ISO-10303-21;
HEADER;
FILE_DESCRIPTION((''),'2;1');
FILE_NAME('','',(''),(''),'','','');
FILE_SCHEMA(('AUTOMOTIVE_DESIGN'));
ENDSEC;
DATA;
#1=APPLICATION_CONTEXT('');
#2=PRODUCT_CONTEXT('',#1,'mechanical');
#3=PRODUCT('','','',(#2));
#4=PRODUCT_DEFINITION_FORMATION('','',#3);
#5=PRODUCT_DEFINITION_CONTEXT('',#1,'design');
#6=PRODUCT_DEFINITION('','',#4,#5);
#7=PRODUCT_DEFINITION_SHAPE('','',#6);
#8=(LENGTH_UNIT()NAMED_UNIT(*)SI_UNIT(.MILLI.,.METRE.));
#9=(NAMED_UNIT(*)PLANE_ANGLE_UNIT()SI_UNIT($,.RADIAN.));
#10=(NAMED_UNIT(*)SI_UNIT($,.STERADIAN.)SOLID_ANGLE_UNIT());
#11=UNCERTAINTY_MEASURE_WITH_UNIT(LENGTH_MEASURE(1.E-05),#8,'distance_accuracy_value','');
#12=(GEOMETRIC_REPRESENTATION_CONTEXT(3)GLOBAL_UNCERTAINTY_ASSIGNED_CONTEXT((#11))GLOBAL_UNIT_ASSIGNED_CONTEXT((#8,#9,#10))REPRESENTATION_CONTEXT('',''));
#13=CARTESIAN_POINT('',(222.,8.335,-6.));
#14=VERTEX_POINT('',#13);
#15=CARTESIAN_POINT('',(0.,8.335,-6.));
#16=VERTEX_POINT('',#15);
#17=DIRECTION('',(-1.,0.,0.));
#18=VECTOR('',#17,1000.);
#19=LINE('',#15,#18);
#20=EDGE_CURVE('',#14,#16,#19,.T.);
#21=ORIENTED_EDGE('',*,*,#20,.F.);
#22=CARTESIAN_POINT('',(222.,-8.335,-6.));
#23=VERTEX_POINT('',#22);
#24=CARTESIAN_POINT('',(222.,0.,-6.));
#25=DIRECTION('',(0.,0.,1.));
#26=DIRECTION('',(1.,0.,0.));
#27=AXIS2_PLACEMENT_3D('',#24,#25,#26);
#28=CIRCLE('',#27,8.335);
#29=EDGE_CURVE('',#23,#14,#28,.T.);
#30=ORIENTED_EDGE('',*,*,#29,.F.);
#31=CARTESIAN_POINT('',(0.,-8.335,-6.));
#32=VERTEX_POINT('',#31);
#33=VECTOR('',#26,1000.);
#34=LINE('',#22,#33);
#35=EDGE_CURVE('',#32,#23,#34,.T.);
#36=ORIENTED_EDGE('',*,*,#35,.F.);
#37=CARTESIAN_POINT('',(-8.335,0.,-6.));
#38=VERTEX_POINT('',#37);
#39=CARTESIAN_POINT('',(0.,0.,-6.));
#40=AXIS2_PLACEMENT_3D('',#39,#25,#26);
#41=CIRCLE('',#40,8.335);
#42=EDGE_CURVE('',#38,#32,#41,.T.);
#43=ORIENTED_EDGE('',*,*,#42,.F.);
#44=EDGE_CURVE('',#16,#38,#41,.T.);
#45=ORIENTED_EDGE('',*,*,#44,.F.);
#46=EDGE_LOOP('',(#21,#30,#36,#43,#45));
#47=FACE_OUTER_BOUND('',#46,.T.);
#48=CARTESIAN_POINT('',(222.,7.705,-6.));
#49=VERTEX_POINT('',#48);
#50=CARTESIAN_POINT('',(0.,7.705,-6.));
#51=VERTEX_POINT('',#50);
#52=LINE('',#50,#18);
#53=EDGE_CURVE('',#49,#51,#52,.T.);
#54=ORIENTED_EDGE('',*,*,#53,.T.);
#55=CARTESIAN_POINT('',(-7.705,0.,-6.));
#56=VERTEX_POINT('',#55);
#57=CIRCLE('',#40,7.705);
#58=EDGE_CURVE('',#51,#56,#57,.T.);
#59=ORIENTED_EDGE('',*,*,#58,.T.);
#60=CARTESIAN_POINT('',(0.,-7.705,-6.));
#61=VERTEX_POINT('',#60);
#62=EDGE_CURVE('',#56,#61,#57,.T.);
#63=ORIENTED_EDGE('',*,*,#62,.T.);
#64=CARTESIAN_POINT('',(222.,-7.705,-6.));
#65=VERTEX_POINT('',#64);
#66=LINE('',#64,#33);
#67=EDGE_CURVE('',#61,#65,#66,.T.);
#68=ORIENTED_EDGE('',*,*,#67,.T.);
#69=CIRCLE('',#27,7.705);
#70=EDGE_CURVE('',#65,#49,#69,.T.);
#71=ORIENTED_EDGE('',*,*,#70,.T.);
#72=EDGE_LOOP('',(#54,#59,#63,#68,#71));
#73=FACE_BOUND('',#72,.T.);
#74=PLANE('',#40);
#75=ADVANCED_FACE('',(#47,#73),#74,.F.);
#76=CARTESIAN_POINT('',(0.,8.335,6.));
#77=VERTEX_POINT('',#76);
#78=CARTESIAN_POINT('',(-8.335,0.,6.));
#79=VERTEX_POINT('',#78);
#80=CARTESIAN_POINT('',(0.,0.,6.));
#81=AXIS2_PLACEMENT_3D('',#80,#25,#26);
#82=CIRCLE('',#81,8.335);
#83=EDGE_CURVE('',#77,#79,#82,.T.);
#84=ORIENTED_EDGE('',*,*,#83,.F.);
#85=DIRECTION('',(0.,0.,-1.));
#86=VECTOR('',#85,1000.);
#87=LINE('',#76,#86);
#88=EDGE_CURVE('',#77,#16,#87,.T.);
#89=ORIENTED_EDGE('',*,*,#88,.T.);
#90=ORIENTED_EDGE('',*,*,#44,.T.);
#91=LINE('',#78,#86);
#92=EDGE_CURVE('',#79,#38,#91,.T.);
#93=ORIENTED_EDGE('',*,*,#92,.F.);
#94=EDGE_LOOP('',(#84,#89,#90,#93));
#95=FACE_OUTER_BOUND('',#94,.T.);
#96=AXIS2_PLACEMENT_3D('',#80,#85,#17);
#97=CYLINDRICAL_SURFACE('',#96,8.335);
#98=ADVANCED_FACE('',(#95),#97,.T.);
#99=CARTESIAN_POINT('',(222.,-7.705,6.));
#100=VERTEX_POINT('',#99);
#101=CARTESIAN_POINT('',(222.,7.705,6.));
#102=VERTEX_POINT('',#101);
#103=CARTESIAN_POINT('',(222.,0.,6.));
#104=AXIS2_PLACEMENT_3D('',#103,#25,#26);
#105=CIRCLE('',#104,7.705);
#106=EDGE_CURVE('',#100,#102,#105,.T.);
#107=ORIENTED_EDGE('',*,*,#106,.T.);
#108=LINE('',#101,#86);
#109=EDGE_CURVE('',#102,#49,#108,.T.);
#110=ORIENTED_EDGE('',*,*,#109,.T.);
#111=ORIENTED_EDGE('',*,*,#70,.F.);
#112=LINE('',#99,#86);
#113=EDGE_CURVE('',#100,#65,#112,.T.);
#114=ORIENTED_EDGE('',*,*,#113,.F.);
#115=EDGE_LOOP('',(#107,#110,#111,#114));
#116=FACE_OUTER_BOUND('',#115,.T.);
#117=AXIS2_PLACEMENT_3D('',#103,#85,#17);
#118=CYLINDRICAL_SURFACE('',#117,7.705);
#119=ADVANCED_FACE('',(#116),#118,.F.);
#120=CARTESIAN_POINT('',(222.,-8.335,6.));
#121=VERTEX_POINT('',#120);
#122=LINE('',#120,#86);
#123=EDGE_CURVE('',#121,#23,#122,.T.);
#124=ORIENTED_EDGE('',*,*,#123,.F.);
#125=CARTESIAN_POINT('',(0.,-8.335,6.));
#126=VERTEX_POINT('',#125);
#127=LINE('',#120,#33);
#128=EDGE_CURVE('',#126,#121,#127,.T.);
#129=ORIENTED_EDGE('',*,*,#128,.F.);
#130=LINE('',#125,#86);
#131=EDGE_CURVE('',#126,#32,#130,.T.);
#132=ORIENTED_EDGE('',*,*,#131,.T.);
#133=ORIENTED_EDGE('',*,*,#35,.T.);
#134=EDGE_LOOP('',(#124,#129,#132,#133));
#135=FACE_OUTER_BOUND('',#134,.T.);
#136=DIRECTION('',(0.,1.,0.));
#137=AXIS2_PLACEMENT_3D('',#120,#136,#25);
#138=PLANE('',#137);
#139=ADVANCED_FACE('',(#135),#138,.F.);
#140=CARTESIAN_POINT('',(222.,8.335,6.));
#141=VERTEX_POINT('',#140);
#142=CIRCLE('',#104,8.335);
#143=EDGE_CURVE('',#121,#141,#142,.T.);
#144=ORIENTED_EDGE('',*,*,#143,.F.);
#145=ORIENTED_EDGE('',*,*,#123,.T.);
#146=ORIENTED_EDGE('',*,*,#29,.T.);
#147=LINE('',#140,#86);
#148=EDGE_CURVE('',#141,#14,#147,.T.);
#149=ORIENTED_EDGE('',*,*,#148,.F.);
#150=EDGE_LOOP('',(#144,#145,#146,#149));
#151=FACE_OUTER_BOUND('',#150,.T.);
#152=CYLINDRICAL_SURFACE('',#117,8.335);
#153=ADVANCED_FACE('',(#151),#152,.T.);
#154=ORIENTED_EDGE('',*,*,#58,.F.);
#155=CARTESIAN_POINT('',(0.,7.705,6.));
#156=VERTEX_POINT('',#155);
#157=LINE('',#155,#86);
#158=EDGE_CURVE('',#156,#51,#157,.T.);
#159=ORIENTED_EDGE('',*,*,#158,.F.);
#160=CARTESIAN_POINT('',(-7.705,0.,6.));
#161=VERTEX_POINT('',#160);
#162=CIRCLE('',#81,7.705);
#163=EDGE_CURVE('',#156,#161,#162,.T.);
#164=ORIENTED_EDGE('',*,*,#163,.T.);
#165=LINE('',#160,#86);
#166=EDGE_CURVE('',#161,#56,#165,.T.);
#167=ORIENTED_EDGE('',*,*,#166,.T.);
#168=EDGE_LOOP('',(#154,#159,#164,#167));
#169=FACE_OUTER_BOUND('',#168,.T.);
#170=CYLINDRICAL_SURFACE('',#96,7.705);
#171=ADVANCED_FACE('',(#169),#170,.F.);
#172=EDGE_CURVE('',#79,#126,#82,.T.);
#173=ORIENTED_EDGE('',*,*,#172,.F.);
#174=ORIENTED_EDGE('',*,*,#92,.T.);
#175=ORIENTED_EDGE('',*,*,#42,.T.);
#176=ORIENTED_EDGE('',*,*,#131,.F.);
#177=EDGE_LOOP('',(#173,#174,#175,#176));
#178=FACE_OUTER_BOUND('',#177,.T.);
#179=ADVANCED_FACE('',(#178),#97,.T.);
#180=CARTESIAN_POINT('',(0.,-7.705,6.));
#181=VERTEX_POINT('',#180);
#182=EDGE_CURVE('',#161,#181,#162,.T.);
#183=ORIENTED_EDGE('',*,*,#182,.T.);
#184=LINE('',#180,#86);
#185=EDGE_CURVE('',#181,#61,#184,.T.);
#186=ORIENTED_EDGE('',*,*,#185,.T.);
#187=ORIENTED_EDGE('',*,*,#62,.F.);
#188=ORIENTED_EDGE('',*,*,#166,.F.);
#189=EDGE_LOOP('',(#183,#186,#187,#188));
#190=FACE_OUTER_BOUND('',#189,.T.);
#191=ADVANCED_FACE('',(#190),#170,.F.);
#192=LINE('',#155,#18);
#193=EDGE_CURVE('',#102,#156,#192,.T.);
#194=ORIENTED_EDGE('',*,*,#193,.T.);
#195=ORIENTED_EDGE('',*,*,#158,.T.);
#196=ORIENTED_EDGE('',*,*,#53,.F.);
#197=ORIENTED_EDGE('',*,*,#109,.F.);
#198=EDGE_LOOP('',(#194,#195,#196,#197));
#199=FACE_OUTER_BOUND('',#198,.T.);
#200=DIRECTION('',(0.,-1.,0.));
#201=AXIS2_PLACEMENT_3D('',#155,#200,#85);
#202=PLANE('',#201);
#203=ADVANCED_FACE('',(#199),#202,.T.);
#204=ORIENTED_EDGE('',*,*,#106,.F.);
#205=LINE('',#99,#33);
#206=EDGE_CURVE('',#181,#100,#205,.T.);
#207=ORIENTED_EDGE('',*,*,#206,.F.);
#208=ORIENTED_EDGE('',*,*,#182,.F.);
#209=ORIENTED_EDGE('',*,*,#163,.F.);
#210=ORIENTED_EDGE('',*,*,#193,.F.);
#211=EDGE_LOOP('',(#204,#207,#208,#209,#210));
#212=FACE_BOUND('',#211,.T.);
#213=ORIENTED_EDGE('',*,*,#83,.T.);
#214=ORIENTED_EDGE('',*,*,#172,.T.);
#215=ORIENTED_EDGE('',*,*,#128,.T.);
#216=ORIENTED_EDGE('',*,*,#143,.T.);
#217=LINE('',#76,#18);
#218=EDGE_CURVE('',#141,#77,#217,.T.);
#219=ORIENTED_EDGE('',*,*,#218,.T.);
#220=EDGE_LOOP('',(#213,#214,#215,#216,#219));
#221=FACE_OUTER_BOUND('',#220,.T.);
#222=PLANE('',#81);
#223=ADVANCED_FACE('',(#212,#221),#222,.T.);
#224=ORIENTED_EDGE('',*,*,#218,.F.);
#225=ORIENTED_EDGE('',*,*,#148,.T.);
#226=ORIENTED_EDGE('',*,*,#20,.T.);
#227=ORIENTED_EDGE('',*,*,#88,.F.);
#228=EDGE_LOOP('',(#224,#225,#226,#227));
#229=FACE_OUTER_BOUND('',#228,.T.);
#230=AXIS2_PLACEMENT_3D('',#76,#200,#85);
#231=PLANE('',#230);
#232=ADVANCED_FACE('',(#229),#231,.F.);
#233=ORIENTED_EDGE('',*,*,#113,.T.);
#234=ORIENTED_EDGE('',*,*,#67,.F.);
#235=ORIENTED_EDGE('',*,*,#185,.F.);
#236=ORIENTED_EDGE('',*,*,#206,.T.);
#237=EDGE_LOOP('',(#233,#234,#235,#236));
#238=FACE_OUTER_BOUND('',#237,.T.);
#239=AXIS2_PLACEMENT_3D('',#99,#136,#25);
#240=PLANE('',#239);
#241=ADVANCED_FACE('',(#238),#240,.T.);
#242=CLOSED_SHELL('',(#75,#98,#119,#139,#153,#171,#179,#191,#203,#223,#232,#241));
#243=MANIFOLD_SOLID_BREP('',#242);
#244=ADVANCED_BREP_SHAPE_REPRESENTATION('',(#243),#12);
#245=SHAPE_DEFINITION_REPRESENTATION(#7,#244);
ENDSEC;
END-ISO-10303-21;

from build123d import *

# Parameters (mm, degrees)
EXTRUDE_1_DEPTH = 6


with BuildPart() as part:
    # 草图1 → 凸台-拉伸1 (new, symmetric)
    with BuildSketch(Plane.XY):
        with BuildLine():
            Line((0, 8.335), (222, 8.335))
            ThreePointArc((222, 8.335), (230.335, 0), (222, -8.335))
            Line((222, -8.335), (0, -8.335))
            ThreePointArc((0, -8.335), (-8.335, 0), (0, 8.335))
        make_face()
        with BuildLine():
            Line((0, 7.705), (222, 7.705))
            ThreePointArc((222, 7.705), (229.705, 0), (222, -7.705))
            Line((222, -7.705), (0, -7.705))
            ThreePointArc((0, -7.705), (-7.705, 0), (0, 7.705))
        make_face(mode=Mode.SUBTRACT)
    extrude(amount=EXTRUDE_1_DEPTH, both=True)


solid = part.part
